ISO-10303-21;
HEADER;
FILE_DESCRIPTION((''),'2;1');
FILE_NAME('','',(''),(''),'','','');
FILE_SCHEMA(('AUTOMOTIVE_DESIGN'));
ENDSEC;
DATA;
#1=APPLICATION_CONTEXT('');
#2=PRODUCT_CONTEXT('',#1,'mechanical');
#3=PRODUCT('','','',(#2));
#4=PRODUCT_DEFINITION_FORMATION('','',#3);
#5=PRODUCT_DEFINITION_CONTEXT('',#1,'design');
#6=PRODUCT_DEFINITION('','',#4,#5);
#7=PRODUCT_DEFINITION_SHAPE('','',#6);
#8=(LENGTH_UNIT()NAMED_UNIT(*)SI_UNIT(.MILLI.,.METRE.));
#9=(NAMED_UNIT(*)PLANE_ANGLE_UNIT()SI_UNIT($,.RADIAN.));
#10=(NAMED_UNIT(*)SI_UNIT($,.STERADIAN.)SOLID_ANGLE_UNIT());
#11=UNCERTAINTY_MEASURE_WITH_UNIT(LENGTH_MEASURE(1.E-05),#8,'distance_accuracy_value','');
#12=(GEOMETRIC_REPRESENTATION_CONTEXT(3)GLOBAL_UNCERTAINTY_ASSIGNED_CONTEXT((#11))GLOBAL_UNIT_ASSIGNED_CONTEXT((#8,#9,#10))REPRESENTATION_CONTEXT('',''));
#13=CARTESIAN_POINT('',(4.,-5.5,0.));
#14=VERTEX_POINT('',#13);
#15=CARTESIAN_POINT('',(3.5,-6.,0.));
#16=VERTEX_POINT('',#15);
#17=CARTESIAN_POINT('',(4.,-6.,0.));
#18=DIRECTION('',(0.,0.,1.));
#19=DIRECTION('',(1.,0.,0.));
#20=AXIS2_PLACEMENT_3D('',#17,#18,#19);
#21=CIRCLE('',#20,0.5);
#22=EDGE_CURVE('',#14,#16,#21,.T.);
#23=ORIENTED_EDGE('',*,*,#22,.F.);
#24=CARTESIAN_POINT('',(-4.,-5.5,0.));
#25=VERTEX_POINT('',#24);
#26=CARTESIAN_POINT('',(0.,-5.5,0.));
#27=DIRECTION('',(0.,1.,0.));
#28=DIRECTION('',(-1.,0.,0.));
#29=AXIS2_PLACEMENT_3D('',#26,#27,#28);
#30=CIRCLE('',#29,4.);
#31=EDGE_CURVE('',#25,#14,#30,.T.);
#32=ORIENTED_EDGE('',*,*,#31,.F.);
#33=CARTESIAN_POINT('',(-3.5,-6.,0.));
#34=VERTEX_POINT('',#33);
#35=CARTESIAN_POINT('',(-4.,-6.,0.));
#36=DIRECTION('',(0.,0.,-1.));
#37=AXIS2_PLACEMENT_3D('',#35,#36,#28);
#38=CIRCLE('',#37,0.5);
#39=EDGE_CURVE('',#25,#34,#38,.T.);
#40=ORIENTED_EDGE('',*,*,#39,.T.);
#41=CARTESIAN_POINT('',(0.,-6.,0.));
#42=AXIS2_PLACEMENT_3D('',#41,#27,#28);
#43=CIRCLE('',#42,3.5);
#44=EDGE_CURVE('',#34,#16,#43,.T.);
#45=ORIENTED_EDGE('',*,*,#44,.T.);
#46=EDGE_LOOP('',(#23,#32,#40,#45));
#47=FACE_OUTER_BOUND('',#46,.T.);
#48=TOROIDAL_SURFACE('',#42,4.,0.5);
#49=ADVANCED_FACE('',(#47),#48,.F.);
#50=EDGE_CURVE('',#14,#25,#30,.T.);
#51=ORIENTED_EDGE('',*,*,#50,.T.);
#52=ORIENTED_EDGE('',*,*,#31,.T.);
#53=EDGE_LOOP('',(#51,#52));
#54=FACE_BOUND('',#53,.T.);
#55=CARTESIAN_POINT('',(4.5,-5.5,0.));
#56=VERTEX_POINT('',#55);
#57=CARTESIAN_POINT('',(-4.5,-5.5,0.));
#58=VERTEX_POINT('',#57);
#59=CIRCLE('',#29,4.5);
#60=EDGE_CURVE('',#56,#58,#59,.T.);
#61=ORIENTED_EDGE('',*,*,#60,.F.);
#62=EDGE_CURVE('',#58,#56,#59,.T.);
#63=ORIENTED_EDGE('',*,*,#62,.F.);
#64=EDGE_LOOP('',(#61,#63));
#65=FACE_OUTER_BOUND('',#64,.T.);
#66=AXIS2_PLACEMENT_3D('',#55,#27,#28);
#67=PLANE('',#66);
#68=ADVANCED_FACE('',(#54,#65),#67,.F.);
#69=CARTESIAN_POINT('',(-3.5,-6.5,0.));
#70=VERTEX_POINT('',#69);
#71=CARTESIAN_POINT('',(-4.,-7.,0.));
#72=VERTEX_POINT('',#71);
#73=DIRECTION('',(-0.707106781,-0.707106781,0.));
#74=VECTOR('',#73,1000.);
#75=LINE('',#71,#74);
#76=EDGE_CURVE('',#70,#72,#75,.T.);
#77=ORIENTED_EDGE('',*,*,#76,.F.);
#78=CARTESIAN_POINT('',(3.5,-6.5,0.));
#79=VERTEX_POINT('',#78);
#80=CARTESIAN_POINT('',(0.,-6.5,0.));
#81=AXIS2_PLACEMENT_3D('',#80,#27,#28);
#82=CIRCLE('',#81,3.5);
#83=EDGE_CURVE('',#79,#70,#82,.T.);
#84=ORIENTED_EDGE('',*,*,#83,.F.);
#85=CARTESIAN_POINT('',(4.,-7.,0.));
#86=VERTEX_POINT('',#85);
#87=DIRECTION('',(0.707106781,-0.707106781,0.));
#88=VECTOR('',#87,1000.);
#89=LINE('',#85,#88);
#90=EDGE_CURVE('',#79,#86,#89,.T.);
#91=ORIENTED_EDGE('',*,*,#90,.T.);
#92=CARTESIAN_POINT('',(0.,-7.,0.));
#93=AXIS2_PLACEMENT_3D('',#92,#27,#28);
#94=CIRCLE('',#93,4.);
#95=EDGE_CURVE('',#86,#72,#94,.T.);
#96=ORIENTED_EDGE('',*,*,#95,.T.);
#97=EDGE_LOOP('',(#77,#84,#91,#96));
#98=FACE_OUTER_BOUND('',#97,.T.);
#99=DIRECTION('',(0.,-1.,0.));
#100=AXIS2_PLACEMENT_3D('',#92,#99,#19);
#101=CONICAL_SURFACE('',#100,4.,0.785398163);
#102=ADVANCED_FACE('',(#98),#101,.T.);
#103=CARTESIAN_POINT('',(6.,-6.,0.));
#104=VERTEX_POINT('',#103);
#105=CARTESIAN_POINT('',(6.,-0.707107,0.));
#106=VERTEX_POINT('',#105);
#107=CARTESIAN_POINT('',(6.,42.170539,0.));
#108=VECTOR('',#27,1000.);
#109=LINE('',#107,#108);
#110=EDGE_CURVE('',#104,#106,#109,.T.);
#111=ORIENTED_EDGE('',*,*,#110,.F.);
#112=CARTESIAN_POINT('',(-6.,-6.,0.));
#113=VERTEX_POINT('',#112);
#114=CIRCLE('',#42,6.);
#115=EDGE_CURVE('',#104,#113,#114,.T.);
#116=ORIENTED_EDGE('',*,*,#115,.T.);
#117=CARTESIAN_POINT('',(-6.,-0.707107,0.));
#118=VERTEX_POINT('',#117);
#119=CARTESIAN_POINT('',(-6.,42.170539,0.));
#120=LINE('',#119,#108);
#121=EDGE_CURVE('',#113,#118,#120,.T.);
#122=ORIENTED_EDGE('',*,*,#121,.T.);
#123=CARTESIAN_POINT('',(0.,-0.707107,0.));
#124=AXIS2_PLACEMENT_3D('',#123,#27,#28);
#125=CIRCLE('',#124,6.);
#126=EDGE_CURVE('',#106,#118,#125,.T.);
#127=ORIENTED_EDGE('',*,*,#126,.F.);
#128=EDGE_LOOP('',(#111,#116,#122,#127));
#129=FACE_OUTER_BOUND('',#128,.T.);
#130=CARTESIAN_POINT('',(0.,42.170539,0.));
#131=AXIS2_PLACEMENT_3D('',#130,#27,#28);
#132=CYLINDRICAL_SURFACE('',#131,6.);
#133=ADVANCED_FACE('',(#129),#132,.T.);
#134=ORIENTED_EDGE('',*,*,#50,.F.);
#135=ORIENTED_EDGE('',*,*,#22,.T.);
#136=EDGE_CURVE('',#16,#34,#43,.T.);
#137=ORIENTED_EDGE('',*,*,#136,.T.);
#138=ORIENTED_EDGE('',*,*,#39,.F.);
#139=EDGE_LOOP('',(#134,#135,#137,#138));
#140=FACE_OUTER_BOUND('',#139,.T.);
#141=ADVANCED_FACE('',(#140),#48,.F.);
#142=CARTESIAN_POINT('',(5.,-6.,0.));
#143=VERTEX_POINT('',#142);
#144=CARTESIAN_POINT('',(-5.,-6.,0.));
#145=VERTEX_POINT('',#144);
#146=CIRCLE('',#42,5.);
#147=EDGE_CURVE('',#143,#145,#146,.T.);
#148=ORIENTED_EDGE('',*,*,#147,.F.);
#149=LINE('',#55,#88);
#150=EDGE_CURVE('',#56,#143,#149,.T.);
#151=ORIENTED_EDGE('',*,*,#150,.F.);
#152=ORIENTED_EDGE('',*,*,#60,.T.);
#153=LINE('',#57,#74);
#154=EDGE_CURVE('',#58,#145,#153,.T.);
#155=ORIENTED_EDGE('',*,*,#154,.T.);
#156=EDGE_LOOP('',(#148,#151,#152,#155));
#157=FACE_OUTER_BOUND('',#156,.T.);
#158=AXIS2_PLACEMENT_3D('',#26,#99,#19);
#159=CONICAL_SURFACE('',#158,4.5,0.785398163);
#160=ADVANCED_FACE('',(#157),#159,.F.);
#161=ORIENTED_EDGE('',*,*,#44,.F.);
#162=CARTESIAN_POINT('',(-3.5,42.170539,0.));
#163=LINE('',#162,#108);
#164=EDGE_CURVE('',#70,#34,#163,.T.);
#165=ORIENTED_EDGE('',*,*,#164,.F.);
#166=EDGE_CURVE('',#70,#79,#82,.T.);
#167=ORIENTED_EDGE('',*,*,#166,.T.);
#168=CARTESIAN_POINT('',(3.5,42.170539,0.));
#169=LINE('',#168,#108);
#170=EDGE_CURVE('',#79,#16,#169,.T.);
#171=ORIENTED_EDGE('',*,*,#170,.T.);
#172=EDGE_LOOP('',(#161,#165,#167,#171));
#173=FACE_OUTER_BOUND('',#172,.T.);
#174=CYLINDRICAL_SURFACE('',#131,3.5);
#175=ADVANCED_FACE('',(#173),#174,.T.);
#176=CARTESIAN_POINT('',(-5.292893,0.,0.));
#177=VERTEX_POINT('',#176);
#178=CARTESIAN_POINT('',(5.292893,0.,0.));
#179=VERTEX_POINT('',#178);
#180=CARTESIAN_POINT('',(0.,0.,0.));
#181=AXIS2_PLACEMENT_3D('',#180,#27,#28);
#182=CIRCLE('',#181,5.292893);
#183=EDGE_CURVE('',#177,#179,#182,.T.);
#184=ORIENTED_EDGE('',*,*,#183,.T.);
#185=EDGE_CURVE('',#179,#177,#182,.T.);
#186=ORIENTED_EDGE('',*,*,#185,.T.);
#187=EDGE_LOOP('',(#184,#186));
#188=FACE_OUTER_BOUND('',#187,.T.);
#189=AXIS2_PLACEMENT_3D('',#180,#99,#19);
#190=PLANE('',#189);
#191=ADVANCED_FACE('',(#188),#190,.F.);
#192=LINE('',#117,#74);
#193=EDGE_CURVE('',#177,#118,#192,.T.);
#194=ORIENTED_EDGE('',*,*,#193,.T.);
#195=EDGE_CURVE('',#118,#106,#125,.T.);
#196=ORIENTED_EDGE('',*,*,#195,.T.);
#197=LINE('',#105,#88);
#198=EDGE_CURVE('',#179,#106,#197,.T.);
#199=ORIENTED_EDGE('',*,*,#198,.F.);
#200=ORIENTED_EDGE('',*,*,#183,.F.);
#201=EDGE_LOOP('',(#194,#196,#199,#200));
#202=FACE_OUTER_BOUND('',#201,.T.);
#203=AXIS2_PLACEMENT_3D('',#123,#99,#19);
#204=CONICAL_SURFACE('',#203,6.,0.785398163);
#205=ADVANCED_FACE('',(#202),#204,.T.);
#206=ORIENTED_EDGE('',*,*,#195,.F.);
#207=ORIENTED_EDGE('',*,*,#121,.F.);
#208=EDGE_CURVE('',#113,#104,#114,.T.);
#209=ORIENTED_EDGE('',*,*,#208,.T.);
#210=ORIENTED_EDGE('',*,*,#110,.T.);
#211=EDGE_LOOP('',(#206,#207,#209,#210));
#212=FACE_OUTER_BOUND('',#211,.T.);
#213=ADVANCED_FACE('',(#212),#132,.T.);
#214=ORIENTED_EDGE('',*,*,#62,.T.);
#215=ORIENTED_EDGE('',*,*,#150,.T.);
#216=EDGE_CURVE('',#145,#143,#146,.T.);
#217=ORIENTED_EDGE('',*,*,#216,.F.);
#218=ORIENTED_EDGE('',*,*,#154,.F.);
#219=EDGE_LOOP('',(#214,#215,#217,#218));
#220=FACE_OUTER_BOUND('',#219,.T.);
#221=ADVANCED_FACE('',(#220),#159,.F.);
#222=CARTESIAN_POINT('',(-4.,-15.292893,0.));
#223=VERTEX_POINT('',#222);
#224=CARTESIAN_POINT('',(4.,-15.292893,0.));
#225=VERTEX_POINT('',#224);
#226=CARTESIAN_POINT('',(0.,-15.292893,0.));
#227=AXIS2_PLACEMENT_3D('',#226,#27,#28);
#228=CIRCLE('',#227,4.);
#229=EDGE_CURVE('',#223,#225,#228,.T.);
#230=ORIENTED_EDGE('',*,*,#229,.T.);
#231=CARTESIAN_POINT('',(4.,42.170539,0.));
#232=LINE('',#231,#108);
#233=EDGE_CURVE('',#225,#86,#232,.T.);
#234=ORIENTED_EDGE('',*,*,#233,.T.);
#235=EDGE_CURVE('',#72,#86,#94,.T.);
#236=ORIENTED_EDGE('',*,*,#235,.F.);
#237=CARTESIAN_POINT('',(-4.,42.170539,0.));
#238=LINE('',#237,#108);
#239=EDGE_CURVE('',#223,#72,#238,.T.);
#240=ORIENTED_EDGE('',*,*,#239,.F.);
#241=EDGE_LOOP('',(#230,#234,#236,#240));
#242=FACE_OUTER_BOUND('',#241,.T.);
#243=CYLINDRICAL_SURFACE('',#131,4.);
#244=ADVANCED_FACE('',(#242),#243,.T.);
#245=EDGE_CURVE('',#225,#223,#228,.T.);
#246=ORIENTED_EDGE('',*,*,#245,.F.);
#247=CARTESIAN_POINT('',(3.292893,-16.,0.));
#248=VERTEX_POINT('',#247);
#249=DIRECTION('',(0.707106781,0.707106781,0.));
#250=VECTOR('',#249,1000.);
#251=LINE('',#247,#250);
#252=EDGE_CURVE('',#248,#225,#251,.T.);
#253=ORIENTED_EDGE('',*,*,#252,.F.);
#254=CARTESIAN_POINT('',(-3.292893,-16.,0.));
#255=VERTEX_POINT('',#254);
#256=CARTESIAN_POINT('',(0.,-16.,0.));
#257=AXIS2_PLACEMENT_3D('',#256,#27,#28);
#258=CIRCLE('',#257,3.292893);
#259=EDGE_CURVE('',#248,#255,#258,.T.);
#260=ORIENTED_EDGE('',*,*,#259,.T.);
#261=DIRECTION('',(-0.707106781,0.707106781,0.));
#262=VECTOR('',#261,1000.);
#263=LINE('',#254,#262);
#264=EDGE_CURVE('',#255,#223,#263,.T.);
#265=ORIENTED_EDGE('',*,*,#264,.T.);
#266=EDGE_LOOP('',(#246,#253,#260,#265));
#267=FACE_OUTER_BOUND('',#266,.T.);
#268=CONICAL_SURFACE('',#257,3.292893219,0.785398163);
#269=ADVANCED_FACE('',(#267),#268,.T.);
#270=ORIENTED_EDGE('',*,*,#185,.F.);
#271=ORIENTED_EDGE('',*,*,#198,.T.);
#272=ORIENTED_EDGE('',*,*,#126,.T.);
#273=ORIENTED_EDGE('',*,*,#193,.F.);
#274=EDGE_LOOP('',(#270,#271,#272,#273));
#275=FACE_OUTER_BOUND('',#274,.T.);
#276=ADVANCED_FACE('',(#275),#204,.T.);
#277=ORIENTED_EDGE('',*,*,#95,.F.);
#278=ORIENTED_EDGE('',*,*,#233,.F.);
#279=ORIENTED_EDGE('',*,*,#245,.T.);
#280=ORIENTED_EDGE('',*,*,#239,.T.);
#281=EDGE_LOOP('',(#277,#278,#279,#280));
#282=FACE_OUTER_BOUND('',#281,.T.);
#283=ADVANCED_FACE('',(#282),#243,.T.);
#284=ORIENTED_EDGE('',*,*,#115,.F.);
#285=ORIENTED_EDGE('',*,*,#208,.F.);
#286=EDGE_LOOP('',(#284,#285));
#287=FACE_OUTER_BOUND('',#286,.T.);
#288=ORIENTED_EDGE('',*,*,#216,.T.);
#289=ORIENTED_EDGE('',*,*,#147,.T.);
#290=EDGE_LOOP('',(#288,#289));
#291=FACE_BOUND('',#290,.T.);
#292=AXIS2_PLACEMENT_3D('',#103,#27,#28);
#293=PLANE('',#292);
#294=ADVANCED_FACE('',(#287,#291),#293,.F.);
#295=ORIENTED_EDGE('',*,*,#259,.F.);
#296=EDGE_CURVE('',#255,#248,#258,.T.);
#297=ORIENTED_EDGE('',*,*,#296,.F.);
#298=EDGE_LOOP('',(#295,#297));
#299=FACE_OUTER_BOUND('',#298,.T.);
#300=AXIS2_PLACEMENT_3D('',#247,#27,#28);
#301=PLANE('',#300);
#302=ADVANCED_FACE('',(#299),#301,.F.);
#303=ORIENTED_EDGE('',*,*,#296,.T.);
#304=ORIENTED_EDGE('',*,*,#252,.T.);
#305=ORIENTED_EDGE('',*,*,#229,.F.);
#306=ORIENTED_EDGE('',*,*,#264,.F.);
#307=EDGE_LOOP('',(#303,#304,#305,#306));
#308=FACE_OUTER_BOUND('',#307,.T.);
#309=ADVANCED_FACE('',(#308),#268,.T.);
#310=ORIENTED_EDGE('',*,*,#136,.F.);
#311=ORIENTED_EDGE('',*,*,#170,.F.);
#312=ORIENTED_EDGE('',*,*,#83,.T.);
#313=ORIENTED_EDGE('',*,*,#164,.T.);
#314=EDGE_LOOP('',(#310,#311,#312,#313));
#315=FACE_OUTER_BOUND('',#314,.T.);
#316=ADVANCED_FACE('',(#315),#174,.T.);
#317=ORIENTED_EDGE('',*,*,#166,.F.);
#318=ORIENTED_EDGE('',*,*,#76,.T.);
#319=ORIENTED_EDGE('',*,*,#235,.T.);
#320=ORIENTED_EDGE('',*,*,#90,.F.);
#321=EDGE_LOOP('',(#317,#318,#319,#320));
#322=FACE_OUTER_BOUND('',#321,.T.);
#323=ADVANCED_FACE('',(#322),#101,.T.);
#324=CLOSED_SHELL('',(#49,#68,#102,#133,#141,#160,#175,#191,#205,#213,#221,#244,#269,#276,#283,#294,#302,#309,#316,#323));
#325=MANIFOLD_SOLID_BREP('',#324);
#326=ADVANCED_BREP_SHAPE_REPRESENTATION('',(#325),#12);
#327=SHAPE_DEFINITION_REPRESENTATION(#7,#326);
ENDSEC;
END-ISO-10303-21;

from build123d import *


with BuildPart() as part:
    # Sketch1 → Boss-Revolve (revolve)
    with BuildSketch(Plane.XY, mode=Mode.PRIVATE) as boss_revolve_sk:
        with BuildLine():
            Line((0, 0), (5.292893219, 0))
            Line((5.292893219, 0), (6, -0.707106781))
            Line((6, -0.707106781), (6, -6))
            Line((6, -6), (5, -6))
            Line((5, -6), (4.5, -5.5))
            Line((4.5, -5.5), (4, -5.5))
            ThreePointArc((4, -5.5), (3.646446609, -5.646446609), (3.5, -6))
            Line((3.5, -6), (3.5, -6.5))
            Line((3.5, -6.5), (4, -7))
            Line((4, -7), (4, -15.292893219))
            Line((4, -15.292893219), (3.292893219, -16))
            Line((3.292893219, -16), (0, -16))
            Line((0, -16), (0, 0))
        make_face()
    revolve(boss_revolve_sk.sketch.rotate(Axis((0, 42.170539173, 0), (0, -1, 0)), 180), axis=Axis((0, 42.170539173, 0), (0, -1, 0)))


solid = part.part
